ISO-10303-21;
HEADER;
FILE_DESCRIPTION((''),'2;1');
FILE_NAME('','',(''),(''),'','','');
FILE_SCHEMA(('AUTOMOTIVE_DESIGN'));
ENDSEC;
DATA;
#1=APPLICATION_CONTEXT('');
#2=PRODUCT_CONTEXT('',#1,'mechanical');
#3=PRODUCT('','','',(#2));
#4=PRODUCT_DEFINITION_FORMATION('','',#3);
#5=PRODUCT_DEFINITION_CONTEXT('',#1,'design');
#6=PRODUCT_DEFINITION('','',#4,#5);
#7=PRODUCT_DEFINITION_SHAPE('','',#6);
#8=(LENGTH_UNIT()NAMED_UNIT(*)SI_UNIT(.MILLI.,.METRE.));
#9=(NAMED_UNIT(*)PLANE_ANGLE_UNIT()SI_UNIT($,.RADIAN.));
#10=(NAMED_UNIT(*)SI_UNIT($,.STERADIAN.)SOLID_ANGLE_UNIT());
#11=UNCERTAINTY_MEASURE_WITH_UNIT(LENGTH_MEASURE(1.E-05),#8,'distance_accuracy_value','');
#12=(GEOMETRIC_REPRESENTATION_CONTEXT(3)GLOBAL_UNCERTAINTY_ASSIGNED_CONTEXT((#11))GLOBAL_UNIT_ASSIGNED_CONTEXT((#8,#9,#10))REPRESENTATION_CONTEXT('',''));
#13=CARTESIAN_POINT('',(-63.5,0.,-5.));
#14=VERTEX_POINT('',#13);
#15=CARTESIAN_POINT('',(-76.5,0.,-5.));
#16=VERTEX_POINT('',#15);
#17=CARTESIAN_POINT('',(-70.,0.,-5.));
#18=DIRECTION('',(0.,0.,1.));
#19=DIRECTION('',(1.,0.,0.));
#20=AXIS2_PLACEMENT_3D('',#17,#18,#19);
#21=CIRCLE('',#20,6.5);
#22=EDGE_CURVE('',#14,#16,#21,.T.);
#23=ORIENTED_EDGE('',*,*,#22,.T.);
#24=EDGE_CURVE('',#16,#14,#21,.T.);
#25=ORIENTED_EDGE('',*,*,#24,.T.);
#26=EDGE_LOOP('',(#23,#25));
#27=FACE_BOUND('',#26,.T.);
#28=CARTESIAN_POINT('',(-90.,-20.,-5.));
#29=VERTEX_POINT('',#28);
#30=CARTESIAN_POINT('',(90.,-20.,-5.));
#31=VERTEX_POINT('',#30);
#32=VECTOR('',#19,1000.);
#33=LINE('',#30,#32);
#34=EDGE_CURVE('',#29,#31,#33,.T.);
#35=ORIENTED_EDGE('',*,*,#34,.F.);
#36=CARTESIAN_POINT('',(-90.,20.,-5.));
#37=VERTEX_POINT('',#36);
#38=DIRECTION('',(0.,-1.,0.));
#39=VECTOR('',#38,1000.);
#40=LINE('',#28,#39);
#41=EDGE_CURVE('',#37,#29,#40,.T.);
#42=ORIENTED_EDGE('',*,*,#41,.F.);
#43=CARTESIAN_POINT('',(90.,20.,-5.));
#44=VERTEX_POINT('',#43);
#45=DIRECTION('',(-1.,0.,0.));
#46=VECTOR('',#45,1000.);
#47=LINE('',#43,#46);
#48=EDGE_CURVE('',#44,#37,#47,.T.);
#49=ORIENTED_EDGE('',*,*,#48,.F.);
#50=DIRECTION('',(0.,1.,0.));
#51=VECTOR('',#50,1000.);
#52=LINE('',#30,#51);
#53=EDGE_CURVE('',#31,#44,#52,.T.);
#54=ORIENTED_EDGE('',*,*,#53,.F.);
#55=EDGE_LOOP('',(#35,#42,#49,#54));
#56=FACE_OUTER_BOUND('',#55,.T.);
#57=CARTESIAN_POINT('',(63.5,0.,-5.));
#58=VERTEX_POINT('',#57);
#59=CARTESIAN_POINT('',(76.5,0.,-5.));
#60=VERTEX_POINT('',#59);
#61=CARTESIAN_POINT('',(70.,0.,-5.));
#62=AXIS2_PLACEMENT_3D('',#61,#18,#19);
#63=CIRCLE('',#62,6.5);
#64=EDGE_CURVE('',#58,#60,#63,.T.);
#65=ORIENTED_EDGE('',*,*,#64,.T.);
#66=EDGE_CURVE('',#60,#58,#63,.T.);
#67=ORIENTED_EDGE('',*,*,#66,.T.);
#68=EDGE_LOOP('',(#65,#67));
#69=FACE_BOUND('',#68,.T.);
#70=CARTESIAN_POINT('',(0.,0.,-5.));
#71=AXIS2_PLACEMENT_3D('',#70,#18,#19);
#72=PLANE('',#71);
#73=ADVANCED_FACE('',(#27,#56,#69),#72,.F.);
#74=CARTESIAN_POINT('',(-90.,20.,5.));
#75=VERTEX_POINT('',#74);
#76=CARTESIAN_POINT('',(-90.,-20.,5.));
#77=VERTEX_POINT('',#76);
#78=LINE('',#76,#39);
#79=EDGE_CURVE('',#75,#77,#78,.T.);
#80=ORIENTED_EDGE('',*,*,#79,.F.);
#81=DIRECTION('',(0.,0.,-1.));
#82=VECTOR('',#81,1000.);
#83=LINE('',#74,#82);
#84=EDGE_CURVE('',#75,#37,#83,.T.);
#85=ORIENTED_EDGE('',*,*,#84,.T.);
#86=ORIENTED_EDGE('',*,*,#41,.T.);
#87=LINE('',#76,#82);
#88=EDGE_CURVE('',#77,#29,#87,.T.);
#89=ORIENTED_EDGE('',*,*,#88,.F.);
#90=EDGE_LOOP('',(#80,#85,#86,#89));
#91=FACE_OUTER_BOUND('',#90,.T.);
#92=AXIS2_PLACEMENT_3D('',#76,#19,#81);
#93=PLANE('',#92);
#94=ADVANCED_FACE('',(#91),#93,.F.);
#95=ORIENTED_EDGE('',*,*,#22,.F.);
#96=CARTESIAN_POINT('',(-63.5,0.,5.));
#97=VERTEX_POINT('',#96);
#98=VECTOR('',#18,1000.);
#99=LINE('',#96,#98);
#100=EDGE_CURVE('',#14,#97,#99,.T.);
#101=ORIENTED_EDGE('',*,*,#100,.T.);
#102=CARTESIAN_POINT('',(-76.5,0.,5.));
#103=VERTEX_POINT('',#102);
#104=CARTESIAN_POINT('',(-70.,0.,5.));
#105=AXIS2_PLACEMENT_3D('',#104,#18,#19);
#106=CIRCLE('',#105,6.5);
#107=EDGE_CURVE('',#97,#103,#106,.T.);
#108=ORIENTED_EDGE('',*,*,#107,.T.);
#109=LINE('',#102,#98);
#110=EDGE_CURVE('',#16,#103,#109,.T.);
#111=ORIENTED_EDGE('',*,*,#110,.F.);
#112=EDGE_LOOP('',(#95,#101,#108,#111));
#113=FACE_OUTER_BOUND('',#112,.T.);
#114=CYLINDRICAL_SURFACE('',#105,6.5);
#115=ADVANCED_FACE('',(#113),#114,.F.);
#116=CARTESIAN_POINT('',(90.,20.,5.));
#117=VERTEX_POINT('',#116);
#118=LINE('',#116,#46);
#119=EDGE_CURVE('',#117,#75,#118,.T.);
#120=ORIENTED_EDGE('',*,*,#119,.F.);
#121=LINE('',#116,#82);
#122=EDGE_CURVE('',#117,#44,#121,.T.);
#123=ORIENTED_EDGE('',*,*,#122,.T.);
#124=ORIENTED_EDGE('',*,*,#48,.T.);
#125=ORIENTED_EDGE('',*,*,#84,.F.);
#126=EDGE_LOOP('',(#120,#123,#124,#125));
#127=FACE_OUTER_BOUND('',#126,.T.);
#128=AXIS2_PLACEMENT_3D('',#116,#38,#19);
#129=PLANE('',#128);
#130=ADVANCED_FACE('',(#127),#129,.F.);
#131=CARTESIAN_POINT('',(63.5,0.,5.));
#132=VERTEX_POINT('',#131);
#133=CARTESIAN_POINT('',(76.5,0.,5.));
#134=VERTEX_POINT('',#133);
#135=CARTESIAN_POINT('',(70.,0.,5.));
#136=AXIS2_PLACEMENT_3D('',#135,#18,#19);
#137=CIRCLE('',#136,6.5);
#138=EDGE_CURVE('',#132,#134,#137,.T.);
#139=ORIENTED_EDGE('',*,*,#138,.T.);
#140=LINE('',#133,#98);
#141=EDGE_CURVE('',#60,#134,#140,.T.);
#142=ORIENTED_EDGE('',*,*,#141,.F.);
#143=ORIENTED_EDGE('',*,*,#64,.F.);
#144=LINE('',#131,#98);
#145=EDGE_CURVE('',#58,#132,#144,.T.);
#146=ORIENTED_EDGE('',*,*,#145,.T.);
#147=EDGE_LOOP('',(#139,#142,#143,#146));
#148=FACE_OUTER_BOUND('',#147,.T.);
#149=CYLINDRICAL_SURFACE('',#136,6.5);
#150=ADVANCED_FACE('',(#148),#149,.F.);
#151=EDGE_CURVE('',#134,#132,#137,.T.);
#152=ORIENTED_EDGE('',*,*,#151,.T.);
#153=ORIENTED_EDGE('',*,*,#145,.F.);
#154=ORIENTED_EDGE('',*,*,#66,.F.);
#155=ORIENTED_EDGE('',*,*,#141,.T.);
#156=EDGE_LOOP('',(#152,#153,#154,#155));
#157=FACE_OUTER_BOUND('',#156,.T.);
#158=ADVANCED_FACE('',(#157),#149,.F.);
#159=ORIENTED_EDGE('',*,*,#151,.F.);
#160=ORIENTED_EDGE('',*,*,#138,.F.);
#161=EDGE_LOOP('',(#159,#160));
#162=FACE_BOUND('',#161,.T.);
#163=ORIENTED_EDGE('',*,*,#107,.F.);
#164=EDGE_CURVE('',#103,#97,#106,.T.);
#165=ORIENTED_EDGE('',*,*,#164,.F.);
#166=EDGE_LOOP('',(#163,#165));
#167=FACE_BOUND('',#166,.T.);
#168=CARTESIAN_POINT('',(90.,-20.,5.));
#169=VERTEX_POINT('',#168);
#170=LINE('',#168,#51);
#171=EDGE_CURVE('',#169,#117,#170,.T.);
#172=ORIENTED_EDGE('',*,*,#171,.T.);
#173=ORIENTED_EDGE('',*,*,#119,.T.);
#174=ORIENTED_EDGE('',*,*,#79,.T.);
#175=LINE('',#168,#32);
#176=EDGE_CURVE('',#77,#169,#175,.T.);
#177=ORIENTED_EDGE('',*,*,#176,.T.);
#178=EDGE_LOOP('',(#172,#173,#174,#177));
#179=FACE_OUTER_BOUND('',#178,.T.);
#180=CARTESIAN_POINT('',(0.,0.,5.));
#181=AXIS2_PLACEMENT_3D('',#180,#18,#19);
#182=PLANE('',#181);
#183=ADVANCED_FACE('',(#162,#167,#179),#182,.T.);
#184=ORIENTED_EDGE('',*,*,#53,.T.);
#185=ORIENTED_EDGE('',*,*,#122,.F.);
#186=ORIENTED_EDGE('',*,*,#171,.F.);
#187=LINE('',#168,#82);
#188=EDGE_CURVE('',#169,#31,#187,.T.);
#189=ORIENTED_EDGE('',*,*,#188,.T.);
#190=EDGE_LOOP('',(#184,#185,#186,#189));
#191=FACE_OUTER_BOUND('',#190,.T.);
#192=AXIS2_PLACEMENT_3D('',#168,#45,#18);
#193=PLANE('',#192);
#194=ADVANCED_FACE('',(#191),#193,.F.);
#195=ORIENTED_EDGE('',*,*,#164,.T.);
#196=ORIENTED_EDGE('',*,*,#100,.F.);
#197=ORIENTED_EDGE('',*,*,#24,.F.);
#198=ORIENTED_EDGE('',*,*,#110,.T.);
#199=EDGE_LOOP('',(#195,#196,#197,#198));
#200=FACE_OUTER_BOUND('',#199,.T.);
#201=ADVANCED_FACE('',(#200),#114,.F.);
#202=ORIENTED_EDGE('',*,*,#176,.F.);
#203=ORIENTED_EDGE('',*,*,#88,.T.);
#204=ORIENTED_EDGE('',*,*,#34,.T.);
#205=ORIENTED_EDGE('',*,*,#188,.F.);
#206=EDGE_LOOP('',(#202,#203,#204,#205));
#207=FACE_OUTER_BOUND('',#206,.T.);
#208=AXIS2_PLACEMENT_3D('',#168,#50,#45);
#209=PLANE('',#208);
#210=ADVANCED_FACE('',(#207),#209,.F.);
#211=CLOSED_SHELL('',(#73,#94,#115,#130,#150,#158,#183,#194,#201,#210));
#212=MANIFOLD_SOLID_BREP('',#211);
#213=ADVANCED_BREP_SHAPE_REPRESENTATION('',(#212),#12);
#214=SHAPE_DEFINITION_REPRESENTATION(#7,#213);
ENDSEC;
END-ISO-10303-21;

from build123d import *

# Parameters (mm, degrees)
SKETCH1_W                  = 180
SKETCH1_H                  = 40
BOSS_EXTRUDE1_DEPTH        = 5
F_13_0_13_DIAMETER_HOLE1_D = 13


with BuildPart() as part:
    # Sketch1 → Boss-Extrude1 (new, symmetric)
    with BuildSketch(Plane.XY):
        Rectangle(SKETCH1_W, SKETCH1_H)
    extrude(amount=BOSS_EXTRUDE1_DEPTH, both=True)

    # Ø13.0 (13) Diameter Hole1 (through all)
    with Locations(Plane.XY.offset(5)):
        with Locations((-70, 0), (70, 0)):
            Hole(F_13_0_13_DIAMETER_HOLE1_D / 2)


solid = part.part
